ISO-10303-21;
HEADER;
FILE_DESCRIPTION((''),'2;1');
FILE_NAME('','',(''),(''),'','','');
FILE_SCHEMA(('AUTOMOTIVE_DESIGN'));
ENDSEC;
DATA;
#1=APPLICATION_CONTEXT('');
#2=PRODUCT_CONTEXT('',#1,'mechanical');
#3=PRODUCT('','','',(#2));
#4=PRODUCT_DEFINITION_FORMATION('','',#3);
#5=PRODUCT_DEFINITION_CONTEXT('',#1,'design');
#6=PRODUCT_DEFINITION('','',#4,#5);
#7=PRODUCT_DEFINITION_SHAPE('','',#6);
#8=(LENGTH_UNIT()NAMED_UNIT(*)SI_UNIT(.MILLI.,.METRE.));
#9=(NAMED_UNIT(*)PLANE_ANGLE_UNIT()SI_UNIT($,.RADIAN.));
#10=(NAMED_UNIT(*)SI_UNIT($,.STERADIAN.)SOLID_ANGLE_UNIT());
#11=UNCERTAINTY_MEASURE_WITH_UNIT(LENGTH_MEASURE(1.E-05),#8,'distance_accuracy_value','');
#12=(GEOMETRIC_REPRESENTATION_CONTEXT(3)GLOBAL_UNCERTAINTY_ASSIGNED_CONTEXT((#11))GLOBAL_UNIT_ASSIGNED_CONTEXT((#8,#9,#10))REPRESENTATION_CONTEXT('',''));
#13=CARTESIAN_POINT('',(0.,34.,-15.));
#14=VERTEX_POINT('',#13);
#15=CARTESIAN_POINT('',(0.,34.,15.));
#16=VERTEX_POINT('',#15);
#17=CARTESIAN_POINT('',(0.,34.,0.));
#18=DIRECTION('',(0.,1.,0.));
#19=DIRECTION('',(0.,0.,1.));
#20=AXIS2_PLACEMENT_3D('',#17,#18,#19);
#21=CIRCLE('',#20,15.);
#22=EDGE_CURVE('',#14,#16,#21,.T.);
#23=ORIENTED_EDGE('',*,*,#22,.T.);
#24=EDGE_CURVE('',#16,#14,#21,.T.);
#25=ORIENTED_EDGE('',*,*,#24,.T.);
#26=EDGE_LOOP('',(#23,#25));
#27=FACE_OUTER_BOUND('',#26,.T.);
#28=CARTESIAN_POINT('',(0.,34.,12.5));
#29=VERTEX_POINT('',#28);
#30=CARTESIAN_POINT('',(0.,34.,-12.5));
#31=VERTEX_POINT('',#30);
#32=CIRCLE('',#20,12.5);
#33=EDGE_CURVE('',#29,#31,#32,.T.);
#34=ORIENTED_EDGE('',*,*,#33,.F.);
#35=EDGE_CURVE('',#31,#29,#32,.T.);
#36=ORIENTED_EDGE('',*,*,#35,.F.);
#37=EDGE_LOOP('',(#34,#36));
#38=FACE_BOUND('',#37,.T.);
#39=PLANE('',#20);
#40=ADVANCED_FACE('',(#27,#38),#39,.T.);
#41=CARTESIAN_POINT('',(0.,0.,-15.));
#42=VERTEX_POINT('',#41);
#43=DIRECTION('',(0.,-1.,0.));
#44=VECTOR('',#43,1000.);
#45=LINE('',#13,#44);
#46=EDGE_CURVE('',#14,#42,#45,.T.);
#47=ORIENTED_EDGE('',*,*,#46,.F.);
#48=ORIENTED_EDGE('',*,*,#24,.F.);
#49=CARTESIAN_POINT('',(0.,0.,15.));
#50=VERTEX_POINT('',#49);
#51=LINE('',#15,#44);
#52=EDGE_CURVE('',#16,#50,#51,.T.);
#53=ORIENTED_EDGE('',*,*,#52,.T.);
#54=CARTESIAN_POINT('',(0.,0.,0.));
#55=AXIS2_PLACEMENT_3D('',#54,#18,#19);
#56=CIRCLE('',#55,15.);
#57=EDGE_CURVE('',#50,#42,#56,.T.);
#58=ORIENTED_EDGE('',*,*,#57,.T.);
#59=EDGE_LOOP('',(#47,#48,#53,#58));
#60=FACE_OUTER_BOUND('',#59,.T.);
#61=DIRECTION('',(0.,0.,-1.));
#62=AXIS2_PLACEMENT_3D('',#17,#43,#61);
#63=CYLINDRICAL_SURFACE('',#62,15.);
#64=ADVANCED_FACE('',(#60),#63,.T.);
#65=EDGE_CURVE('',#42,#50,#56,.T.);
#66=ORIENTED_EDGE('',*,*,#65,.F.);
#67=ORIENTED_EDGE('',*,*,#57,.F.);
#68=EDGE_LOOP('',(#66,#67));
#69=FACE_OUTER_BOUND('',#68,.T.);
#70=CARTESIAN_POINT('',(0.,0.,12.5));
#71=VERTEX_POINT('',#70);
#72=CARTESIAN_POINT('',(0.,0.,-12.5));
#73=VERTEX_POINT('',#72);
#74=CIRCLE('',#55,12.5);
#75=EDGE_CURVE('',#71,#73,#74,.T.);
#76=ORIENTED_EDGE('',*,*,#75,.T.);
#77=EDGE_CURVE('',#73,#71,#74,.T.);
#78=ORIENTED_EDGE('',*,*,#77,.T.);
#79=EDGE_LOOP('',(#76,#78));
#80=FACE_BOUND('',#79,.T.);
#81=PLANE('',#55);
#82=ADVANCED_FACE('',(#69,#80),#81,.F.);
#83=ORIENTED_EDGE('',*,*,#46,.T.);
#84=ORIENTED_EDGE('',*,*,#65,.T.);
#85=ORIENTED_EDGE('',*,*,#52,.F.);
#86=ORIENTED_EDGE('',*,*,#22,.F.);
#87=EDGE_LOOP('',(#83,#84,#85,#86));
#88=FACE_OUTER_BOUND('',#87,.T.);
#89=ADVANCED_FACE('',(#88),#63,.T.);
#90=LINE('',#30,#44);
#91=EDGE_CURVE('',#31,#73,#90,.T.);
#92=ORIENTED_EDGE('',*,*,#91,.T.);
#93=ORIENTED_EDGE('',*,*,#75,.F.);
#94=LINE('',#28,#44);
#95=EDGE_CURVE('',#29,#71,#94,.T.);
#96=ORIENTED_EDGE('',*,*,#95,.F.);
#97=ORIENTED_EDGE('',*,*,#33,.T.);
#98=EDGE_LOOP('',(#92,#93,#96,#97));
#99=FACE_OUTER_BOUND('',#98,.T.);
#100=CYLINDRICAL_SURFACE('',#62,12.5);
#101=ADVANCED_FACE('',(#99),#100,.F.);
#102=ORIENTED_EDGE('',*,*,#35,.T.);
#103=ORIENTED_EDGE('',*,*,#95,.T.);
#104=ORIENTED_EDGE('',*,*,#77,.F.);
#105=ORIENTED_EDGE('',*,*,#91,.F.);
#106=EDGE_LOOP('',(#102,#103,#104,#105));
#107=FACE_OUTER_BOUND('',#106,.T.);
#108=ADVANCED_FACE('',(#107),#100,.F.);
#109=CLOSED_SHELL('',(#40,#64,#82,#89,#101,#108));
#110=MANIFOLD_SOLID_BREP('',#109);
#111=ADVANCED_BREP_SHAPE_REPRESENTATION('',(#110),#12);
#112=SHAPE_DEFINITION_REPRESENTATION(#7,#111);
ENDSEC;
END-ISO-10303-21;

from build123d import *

# Parameters (mm, degrees)
SKETCH_1_R      = 15
SKETCH_1_R_2    = 12.5
EXTRUDE_1_DEPTH = 34


with BuildPart() as part:
    # 草图1 → 凸台-拉伸1 (new body)
    with BuildSketch(Plane(origin=(0, 0, 0), x_dir=(1, 0, 0), z_dir=(0, 1, 0))):
        with Locations(Location((0, 0, 0), (0, 0, 270))):
            Circle(SKETCH_1_R)
        with Locations(Location((0, 0, 0), (0, 0, 270))):
            Circle(SKETCH_1_R_2, mode=Mode.SUBTRACT)
    extrude(amount=EXTRUDE_1_DEPTH)


solid = part.part
